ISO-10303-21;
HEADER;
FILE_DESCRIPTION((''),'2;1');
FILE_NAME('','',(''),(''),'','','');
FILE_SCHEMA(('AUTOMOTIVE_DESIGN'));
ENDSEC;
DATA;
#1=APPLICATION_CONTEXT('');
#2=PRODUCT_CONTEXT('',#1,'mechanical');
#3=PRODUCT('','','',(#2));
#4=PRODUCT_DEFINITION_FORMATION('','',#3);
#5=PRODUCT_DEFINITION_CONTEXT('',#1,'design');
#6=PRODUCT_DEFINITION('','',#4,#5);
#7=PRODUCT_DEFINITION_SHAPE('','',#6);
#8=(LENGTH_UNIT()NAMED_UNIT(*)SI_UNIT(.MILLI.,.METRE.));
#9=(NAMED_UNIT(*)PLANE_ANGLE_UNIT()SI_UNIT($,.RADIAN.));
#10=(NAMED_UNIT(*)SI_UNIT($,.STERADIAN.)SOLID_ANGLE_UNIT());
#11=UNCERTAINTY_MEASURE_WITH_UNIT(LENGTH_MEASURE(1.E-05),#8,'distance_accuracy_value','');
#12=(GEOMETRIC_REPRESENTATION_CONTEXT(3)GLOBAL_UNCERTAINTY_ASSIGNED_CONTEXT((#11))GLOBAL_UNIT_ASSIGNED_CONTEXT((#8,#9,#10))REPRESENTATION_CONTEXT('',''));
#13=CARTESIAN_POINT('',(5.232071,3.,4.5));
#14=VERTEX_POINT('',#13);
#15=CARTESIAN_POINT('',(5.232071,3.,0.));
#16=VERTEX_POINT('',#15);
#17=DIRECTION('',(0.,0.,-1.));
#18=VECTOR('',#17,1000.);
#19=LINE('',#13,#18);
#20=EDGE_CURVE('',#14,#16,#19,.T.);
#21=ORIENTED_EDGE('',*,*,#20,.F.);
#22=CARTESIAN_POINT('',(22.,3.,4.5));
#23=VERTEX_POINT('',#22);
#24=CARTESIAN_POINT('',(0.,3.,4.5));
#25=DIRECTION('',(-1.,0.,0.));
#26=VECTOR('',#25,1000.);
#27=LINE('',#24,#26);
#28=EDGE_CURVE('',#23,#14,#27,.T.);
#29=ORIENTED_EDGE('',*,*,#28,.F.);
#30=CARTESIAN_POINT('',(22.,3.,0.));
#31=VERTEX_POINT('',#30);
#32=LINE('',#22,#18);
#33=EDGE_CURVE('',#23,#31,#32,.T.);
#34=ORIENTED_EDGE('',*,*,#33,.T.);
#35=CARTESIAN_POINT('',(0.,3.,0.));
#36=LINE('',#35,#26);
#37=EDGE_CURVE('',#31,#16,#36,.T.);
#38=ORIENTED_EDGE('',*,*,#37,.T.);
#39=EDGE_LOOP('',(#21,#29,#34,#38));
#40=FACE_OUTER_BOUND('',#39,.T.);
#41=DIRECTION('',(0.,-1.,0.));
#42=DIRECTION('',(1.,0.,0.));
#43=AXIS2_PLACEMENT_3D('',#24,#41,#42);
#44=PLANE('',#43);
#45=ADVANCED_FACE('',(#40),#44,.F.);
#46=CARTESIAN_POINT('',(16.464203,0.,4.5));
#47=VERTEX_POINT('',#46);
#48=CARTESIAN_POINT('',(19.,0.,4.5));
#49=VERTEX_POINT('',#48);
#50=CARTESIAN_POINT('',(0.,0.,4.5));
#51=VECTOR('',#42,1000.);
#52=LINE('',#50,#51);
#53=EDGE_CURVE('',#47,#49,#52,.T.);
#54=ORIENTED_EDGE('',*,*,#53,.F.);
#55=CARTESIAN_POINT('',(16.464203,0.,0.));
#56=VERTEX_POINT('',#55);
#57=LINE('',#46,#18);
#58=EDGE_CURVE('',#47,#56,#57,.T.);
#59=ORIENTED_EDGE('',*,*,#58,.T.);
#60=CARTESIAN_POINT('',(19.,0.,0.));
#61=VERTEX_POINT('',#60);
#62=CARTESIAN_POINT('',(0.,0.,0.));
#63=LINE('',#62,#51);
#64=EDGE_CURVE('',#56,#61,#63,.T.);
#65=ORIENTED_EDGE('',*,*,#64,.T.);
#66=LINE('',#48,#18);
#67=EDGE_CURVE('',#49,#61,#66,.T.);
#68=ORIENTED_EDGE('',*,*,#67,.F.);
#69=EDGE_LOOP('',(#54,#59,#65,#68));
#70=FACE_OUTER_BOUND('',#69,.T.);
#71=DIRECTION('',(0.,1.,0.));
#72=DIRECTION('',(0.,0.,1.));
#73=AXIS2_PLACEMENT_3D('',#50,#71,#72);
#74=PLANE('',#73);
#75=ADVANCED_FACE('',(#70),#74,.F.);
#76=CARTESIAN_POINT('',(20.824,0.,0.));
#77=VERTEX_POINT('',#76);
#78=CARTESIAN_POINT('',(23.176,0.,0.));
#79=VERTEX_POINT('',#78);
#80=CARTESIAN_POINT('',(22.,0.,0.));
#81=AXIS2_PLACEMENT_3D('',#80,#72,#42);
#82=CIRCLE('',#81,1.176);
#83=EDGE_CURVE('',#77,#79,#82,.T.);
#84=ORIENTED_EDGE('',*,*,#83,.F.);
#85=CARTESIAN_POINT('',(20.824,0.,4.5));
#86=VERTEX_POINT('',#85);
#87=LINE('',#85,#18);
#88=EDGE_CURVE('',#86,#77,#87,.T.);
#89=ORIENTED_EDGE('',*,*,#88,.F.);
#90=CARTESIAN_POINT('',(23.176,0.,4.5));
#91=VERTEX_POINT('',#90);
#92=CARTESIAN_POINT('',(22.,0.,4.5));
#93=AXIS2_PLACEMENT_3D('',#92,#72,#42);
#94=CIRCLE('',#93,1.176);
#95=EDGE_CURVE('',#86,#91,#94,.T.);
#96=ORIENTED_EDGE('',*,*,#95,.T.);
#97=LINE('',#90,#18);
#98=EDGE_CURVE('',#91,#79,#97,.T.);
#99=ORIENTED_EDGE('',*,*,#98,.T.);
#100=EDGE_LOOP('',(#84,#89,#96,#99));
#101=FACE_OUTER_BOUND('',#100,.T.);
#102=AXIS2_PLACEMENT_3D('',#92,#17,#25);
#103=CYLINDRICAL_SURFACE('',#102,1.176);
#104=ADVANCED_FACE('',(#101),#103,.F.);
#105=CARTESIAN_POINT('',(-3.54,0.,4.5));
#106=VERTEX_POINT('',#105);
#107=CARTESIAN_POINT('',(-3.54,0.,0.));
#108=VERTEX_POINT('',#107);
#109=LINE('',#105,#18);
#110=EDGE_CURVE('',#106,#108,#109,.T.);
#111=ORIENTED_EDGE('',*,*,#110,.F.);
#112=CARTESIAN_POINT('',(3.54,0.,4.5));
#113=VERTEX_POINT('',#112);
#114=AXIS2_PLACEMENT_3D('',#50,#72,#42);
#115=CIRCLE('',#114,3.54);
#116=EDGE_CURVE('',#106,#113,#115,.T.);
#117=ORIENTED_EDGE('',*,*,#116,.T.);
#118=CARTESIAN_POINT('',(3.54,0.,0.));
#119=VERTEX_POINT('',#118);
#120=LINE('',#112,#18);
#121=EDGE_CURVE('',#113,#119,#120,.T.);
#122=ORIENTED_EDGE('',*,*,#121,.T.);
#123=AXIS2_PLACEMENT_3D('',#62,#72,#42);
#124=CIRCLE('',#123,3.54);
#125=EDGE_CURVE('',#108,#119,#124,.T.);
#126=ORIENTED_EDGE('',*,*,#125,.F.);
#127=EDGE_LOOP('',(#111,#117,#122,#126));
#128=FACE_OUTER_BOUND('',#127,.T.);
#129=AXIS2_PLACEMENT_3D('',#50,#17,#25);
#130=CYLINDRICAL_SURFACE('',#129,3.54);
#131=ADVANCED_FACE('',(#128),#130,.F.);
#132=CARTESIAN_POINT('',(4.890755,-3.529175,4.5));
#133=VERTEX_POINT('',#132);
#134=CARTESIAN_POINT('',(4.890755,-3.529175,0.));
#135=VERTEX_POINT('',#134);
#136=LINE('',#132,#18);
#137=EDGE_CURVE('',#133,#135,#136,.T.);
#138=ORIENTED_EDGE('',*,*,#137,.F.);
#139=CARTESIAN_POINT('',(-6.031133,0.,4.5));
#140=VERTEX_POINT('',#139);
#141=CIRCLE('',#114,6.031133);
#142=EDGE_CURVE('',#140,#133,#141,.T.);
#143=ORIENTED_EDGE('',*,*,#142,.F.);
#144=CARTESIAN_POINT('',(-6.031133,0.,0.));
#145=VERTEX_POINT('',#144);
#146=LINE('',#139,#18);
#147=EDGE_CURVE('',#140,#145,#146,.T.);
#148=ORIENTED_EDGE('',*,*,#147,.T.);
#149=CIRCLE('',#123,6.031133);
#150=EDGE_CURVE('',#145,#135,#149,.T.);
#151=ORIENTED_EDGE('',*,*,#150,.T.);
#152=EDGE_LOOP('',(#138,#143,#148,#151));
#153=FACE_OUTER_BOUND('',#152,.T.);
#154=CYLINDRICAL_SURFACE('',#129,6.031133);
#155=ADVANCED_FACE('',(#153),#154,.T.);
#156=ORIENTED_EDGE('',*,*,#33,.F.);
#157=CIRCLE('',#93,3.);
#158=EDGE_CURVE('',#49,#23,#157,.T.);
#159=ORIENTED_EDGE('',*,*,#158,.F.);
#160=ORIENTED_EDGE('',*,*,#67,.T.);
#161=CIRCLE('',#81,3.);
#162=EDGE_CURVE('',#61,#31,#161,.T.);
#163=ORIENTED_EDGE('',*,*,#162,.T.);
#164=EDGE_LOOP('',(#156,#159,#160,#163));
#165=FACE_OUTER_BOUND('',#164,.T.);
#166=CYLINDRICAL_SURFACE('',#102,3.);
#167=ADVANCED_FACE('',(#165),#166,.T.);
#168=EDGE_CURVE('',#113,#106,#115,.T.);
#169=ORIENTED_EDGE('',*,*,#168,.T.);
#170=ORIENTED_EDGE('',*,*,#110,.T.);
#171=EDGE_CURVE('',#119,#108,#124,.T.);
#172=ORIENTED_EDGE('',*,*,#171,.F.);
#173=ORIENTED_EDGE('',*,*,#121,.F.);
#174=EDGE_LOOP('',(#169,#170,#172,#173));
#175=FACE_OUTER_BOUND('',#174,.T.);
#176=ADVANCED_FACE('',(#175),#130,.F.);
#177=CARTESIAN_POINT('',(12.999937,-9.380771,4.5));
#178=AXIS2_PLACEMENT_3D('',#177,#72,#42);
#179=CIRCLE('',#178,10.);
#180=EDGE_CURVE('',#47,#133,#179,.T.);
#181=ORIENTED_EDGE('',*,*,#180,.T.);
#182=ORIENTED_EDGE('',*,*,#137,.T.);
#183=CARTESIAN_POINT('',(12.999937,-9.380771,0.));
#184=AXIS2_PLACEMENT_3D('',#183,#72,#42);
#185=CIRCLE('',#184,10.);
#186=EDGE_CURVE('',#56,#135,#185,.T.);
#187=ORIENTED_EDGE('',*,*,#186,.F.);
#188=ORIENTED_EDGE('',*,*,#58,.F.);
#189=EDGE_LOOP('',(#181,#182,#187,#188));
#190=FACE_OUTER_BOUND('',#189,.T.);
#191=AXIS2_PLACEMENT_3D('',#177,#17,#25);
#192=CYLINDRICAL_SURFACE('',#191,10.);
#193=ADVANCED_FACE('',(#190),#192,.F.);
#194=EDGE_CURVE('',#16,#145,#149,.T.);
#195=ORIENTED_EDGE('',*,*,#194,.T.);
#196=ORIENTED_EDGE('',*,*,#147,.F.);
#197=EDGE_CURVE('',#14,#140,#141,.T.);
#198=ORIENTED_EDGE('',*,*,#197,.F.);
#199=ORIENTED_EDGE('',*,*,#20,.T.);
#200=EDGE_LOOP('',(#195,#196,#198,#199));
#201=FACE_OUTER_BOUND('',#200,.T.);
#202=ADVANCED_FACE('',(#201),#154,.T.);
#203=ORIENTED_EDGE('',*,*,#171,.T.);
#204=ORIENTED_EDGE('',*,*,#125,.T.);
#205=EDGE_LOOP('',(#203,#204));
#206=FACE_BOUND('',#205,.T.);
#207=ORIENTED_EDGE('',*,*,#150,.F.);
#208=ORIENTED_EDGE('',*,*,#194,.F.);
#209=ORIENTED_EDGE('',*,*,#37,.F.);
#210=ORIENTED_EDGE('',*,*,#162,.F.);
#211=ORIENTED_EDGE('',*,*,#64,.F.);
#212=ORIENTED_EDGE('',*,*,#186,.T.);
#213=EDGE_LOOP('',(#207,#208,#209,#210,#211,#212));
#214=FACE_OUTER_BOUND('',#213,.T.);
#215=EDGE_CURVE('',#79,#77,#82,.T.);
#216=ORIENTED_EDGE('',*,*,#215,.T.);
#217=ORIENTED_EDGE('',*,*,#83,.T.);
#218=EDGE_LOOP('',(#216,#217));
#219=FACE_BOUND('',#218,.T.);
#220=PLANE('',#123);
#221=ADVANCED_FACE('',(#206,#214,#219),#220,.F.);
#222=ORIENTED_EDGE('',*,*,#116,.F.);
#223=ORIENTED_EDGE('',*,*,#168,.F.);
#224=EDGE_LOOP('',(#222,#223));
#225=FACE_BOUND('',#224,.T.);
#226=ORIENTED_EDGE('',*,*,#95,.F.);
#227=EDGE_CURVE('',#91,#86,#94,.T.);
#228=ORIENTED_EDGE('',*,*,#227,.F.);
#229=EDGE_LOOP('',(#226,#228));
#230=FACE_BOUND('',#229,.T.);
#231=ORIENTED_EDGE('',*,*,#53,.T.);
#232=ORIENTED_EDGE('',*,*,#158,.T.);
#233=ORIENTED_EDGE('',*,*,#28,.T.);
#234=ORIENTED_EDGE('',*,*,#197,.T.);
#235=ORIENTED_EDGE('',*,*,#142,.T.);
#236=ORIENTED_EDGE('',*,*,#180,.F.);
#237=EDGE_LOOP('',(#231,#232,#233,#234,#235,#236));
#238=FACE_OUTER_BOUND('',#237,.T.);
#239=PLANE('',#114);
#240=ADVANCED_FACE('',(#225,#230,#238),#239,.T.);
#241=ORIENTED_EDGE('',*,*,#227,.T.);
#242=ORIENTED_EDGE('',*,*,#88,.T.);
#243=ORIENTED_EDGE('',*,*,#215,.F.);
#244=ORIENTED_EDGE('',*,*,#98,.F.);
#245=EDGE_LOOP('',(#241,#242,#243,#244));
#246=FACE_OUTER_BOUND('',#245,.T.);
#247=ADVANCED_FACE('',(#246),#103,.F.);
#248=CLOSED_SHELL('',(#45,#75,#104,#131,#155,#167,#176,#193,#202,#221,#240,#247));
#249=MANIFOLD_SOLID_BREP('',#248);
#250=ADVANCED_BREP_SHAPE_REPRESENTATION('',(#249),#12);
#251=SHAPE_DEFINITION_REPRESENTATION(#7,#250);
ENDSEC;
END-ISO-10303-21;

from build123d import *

# Parameters (mm, degrees)
SKETCH_1_R      = 3.54
SKETCH_1_R_2    = 1.176
EXTRUDE_1_DEPTH = 4.5


with BuildPart() as part:
    # 草图1 → 凸台-拉伸1 (new body)
    with BuildSketch(Plane.XY):
        with BuildLine():
            Line((22, 3), (5.232070686, 3))
            ThreePointArc((5.232070686, 3), (-6.022909015, 0.314850207), (4.890755195, -3.529175156))
            ThreePointArc((4.890755195, -3.529175156), (10.083161164, 0.184396071), (16.464202545, 0))
            Line((16.464202545, 0), (19, 0))
            ThreePointArc((19, 0), (24.121320344, -2.121320344), (22, 3))
        make_face()
        Circle(SKETCH_1_R, mode=Mode.SUBTRACT)
        with Locations((22, 0)):
            Circle(SKETCH_1_R_2, mode=Mode.SUBTRACT)
    extrude(amount=EXTRUDE_1_DEPTH)


solid = part.part
